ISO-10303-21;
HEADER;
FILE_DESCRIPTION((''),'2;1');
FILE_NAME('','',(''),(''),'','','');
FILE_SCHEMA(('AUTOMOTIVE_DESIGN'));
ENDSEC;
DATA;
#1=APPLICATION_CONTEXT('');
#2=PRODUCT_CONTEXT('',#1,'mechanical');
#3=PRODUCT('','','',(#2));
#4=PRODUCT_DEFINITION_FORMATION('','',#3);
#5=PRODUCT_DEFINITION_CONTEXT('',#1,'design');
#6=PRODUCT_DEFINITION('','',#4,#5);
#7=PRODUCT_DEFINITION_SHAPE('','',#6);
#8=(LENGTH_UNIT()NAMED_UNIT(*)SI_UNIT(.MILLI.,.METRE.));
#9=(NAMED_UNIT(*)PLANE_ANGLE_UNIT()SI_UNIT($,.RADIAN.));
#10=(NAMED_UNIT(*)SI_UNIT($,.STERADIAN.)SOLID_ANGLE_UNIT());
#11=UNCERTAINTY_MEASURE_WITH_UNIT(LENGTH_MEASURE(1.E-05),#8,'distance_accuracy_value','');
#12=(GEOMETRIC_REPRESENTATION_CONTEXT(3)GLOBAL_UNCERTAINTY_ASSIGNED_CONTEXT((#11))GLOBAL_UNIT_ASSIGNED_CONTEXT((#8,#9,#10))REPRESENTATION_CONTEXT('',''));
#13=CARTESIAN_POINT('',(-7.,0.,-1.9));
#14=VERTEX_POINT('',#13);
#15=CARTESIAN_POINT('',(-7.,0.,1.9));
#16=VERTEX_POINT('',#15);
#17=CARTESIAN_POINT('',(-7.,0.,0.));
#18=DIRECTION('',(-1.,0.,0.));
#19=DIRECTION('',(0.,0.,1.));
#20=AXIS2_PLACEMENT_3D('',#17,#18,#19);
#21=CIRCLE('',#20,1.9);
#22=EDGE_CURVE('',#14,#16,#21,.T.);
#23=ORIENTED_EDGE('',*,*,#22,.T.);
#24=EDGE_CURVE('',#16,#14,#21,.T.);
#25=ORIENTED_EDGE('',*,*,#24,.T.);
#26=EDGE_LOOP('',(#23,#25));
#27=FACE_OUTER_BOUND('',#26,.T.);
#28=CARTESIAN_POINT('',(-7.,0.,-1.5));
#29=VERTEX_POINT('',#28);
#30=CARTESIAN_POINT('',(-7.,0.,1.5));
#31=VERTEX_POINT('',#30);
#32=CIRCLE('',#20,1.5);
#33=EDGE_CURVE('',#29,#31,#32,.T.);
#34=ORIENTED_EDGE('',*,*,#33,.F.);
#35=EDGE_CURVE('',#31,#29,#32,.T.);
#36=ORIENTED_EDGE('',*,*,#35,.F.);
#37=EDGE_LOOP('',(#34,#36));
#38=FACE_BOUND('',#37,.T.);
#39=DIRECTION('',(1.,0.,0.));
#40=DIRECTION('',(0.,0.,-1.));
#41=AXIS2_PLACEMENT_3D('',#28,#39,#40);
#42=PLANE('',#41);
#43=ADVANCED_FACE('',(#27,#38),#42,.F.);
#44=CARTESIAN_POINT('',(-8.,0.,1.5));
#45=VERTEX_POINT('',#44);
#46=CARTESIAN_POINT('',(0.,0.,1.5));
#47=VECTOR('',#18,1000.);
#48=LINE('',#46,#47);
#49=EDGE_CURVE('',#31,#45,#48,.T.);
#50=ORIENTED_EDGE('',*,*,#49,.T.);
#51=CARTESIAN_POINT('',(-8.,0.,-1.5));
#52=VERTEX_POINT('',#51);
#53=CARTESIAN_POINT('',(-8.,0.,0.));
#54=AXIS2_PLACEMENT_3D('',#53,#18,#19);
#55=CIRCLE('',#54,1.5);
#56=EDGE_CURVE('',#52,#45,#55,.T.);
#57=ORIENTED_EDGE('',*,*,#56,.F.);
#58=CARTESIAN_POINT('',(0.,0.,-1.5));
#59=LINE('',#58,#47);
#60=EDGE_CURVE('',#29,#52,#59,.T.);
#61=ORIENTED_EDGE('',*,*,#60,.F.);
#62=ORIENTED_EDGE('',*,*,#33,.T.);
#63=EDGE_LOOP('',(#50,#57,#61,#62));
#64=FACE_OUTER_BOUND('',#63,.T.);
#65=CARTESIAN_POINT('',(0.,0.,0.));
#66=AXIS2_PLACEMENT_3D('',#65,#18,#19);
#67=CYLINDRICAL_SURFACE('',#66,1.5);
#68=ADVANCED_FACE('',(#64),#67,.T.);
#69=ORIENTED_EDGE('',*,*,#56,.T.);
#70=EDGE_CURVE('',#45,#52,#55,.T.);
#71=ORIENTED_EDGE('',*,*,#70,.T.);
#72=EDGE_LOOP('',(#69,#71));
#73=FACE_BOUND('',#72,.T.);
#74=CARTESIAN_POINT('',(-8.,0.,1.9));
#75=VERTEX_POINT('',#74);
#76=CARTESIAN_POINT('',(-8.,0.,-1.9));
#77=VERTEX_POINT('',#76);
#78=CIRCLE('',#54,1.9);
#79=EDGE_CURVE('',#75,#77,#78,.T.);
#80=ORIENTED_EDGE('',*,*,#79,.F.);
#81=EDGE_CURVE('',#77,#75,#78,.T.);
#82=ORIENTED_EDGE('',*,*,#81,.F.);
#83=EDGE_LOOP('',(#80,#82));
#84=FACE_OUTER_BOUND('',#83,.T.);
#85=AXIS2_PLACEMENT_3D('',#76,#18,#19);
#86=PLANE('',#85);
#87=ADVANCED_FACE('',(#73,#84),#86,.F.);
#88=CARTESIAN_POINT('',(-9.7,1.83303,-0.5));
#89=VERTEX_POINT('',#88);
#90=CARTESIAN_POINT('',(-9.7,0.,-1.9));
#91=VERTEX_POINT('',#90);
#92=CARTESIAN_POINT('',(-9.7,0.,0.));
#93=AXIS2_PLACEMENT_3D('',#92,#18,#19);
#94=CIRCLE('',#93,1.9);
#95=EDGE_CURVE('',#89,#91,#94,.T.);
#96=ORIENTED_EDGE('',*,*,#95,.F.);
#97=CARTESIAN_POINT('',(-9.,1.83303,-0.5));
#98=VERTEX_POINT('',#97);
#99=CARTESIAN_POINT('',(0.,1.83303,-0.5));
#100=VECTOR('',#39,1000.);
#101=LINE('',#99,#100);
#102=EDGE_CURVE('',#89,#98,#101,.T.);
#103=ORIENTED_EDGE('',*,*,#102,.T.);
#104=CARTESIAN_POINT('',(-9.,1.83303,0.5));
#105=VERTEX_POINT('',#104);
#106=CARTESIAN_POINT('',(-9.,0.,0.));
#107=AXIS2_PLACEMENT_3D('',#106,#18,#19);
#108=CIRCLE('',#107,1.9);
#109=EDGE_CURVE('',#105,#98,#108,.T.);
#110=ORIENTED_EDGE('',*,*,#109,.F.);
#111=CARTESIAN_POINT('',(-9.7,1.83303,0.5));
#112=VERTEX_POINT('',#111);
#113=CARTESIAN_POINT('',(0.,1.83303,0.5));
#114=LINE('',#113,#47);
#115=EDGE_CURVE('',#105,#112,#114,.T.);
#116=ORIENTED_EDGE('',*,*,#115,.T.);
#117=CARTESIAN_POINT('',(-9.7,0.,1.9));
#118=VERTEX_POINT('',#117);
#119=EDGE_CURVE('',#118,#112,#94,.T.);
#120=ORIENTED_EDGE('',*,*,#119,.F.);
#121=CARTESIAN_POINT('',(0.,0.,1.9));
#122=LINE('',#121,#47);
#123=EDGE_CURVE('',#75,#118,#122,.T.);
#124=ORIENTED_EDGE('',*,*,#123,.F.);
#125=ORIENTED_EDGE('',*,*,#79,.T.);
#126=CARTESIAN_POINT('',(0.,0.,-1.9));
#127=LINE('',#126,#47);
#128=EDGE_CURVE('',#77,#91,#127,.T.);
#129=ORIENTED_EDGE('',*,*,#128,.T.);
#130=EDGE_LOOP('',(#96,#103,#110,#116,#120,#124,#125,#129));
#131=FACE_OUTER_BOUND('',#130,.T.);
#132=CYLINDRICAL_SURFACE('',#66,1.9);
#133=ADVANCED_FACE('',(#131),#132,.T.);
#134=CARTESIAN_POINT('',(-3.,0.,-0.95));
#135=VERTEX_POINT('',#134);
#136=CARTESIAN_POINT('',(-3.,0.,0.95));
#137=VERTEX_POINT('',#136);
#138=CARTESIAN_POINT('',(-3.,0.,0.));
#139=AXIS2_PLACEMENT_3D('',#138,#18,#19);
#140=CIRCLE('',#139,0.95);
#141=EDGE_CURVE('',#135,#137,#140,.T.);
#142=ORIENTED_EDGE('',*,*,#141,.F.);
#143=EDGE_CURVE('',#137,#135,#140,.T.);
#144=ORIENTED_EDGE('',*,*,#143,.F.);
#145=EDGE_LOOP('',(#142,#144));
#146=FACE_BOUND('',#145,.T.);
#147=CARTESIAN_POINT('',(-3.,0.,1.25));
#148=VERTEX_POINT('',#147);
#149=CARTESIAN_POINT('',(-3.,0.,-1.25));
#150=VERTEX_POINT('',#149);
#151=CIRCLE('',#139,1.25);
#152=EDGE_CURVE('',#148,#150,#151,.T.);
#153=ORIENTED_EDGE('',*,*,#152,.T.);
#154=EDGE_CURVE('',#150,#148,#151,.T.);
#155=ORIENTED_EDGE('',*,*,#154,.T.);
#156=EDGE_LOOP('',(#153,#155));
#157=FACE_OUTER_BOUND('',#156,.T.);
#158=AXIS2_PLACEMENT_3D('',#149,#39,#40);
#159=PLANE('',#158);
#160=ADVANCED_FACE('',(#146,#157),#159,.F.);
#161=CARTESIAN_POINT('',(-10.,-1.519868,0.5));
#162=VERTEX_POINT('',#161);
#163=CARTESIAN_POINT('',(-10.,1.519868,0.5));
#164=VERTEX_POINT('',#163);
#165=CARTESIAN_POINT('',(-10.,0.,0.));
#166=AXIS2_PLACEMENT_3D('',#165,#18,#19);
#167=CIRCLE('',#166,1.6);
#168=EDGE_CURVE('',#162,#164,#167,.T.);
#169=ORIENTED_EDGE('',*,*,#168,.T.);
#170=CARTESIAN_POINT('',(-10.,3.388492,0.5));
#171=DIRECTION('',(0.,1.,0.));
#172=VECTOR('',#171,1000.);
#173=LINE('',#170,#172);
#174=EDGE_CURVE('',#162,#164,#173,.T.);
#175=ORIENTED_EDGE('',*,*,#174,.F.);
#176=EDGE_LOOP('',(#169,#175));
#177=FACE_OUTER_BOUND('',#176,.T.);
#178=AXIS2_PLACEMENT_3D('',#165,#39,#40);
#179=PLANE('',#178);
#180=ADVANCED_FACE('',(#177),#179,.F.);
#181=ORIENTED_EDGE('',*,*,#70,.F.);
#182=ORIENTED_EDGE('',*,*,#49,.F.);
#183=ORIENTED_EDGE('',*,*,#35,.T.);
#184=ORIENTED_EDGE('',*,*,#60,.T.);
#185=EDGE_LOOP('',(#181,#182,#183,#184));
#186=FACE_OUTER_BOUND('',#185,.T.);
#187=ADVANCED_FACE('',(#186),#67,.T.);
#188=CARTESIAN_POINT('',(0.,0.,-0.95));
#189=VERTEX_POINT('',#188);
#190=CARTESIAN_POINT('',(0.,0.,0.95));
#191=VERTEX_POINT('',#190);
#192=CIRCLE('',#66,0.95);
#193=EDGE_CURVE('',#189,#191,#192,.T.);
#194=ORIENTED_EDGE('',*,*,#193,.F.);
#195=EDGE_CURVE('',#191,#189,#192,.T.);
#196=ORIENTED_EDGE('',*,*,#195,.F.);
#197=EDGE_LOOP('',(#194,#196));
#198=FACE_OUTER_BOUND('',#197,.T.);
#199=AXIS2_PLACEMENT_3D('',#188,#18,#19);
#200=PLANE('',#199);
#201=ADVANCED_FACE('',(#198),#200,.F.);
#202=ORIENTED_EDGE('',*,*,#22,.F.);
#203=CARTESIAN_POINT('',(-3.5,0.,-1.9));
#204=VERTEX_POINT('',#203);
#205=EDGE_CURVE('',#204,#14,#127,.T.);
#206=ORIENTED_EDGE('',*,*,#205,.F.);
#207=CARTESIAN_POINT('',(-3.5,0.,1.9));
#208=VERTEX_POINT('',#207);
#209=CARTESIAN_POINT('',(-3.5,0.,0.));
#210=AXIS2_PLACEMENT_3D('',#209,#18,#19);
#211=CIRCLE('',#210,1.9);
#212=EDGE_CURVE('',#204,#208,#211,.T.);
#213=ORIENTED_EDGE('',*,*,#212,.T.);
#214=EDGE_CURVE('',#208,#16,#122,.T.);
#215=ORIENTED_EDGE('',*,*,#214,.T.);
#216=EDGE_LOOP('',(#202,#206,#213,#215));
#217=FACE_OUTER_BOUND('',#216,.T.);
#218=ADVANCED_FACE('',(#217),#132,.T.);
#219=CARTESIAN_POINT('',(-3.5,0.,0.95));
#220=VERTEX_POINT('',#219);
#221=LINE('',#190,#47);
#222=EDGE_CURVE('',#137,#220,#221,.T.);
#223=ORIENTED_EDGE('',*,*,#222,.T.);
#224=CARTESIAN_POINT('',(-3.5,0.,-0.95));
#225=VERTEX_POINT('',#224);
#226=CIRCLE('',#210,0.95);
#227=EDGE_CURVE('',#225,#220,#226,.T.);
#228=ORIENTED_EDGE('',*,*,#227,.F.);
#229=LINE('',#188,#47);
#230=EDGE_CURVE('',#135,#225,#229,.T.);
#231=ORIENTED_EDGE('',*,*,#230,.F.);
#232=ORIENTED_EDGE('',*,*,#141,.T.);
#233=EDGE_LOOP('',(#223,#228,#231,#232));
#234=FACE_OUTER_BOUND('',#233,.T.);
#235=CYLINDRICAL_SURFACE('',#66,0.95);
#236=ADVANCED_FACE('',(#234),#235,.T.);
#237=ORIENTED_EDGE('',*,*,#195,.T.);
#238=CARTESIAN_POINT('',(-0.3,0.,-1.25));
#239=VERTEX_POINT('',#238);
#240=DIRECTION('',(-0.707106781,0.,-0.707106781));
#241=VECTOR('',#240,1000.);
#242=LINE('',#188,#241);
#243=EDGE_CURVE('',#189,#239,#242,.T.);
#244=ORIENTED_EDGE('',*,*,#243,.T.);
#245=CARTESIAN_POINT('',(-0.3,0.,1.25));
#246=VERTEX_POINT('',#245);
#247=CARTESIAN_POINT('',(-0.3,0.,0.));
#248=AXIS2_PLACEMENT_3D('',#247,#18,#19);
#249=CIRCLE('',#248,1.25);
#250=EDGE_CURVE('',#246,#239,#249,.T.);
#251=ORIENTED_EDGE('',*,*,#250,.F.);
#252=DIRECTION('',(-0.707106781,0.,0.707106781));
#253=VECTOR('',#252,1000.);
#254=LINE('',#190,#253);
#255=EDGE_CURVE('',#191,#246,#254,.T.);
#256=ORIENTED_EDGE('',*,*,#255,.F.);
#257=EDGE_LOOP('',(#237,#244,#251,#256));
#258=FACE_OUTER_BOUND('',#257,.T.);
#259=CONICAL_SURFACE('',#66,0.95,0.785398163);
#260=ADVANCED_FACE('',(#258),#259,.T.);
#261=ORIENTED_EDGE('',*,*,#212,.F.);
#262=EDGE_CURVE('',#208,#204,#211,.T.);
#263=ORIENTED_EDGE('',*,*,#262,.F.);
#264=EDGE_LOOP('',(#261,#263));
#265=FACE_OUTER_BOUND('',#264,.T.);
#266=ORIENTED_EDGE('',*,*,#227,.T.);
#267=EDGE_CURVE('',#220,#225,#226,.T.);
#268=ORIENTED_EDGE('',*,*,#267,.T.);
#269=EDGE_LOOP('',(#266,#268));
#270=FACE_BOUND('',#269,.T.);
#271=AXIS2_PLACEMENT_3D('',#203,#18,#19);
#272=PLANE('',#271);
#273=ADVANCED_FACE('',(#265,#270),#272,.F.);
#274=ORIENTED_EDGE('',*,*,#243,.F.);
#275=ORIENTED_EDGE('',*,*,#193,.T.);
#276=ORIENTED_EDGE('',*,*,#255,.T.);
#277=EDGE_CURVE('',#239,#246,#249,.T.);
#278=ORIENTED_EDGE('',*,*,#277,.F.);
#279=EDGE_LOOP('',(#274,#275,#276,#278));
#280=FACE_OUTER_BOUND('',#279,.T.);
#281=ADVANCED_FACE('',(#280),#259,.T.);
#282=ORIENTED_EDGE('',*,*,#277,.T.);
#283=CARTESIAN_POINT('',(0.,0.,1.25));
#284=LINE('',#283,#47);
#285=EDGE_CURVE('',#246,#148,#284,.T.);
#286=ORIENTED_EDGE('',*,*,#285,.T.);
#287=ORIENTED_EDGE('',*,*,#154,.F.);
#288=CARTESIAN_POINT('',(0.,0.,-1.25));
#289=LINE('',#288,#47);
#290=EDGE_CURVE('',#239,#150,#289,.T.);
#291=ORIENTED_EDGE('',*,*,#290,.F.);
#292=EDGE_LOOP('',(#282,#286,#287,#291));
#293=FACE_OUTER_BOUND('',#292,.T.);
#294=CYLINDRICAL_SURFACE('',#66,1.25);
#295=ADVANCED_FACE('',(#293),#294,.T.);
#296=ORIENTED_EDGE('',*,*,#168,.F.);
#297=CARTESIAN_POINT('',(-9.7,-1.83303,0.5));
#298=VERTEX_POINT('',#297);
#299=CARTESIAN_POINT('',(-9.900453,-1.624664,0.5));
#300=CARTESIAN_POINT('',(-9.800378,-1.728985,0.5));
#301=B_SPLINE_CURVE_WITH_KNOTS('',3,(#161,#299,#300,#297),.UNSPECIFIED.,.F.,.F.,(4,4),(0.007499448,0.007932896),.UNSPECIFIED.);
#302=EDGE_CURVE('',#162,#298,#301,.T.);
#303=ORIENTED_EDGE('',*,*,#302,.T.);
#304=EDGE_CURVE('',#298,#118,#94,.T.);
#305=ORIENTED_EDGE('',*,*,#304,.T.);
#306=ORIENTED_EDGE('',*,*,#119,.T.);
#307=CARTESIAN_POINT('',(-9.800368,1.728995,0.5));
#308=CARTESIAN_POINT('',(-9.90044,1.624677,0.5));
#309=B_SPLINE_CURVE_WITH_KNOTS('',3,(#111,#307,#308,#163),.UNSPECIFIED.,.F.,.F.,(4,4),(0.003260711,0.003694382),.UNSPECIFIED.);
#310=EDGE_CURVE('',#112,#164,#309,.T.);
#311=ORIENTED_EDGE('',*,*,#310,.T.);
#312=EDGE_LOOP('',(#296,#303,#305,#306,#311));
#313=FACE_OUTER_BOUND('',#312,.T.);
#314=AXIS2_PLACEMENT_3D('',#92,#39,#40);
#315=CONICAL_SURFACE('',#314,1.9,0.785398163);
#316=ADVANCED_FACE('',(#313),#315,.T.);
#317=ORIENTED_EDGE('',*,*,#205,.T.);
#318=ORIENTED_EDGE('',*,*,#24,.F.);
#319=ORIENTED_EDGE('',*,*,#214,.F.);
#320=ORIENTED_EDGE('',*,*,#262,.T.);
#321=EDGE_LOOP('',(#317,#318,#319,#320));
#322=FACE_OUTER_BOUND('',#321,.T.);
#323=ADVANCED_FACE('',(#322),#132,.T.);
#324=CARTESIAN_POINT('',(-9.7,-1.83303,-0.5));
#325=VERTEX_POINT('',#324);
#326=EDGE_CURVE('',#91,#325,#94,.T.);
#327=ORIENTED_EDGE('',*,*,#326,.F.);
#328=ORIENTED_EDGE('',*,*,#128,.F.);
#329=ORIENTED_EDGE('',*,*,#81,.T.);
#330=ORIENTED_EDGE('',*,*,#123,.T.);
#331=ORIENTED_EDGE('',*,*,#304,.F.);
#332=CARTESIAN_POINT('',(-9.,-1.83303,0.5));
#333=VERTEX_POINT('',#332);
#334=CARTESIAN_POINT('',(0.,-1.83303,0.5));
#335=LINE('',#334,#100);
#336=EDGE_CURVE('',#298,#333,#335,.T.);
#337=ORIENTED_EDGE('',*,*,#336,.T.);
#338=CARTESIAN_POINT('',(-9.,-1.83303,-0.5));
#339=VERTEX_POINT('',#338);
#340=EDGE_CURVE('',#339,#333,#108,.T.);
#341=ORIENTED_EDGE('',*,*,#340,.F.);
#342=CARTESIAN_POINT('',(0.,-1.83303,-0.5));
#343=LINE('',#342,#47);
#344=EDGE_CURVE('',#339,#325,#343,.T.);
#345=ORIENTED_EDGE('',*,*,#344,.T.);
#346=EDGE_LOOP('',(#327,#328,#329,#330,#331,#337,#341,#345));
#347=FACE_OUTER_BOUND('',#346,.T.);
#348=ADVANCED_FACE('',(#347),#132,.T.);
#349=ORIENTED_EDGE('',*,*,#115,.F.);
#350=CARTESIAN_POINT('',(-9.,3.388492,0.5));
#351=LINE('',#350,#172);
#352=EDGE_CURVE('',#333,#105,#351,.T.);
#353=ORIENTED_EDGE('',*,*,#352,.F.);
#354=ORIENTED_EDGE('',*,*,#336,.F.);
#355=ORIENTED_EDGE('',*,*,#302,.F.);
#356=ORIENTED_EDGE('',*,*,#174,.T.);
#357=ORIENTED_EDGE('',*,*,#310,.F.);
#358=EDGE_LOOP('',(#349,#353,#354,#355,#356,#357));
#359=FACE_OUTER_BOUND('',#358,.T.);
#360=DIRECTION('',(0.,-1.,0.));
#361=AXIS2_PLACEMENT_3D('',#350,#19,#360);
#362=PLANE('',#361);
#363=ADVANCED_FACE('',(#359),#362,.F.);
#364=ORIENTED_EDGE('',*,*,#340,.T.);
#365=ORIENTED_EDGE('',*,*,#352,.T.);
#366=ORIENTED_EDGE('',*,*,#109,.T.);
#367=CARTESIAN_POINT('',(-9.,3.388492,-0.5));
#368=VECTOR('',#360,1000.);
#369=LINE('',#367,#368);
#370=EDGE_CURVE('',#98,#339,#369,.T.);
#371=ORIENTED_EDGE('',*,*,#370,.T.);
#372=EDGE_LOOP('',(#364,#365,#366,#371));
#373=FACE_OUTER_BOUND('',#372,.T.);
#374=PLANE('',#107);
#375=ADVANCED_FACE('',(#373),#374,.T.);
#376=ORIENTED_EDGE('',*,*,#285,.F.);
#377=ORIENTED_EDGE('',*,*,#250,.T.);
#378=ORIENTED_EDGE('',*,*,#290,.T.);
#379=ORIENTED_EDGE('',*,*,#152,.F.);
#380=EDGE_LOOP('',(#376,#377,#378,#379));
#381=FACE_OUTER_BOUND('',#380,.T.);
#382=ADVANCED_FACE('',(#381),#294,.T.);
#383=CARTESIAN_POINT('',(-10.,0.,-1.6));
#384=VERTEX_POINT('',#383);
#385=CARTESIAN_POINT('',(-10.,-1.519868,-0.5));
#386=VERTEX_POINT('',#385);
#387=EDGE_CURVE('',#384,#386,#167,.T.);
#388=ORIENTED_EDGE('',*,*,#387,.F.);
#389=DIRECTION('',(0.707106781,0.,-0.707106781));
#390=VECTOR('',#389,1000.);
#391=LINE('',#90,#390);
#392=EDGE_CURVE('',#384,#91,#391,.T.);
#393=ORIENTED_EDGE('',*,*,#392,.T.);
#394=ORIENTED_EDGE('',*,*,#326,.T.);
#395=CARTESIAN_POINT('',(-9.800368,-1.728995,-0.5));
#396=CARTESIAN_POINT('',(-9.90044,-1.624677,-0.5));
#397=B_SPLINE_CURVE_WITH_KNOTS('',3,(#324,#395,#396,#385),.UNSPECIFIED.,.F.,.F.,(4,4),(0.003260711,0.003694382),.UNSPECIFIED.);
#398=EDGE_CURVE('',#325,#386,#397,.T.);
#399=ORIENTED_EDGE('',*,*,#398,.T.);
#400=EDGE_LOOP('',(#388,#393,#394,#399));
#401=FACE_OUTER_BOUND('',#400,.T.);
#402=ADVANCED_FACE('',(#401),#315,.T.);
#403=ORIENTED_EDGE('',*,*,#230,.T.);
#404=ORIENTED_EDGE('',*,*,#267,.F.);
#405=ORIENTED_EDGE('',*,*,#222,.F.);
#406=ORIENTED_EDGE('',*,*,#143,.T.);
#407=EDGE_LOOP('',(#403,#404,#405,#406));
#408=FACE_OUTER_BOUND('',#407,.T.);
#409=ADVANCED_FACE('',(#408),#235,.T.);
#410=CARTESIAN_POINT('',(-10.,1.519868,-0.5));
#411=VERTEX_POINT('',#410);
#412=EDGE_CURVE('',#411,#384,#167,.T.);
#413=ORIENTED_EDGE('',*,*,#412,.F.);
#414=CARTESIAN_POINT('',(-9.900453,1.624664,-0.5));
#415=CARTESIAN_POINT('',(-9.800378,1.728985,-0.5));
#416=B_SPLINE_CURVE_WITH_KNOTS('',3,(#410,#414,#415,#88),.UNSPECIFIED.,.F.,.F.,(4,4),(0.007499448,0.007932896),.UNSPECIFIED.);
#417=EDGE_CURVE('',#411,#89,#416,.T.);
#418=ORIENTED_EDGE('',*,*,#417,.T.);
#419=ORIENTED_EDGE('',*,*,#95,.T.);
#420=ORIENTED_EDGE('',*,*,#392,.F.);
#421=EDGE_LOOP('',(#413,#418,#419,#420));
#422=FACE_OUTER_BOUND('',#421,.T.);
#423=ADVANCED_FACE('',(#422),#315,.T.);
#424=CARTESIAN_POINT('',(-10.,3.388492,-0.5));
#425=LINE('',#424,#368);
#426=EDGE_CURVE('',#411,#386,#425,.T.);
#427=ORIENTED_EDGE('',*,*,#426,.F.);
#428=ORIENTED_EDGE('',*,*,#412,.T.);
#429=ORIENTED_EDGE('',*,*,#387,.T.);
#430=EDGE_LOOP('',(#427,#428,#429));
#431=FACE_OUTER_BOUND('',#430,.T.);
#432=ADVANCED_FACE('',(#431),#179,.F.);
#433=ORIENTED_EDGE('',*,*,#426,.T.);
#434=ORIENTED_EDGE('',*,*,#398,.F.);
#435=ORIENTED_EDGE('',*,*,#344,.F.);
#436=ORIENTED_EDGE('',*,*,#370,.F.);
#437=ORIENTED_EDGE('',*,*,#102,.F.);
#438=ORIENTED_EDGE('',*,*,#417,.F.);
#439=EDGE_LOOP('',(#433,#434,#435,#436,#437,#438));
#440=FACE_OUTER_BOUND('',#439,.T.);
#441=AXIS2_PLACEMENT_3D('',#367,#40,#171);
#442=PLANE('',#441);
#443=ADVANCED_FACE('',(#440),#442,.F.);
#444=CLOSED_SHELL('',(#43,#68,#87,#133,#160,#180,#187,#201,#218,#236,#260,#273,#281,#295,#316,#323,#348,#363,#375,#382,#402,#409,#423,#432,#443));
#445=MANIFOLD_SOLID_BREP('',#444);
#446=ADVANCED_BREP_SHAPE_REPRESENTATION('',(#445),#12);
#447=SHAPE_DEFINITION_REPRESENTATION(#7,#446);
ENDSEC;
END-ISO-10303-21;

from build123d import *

# Parameters (mm, degrees)
SKETCH2_W          = 1
SKETCH2_H          = 6.77698326
CUT_EXTRUDE1_DEPTH = 1


with BuildPart() as part:
    # Sketch1 → Revolve1 (revolve)
    with BuildSketch(Plane(origin=(0, 0, 0), x_dir=(1, 0, 0), z_dir=(0, 1, 0)), mode=Mode.PRIVATE) as revolve1_sk:
        Polygon((0, 0), (-10, 0), (-10, 1.6), (-9.7, 1.9), (-8, 1.9), (-8, 1.5), (-7, 1.5), (-7, 1.9), (-3.5, 1.9), (-3.5, 0.95), (-3, 0.95), (-3, 1.25), (-0.3, 1.25), (0, 0.95), align=None)
    revolve(revolve1_sk.sketch.rotate(Axis((0, 0, 0), (1, 0, 0)), 180), axis=Axis((0, 0, 0), (1, 0, 0)))

    # Sketch2 → Cut-Extrude1 (cut)
    with BuildSketch(Plane.ZY.offset(10)):
        Rectangle(SKETCH2_W, SKETCH2_H)
    extrude(amount=-CUT_EXTRUDE1_DEPTH, mode=Mode.SUBTRACT)


solid = part.part
